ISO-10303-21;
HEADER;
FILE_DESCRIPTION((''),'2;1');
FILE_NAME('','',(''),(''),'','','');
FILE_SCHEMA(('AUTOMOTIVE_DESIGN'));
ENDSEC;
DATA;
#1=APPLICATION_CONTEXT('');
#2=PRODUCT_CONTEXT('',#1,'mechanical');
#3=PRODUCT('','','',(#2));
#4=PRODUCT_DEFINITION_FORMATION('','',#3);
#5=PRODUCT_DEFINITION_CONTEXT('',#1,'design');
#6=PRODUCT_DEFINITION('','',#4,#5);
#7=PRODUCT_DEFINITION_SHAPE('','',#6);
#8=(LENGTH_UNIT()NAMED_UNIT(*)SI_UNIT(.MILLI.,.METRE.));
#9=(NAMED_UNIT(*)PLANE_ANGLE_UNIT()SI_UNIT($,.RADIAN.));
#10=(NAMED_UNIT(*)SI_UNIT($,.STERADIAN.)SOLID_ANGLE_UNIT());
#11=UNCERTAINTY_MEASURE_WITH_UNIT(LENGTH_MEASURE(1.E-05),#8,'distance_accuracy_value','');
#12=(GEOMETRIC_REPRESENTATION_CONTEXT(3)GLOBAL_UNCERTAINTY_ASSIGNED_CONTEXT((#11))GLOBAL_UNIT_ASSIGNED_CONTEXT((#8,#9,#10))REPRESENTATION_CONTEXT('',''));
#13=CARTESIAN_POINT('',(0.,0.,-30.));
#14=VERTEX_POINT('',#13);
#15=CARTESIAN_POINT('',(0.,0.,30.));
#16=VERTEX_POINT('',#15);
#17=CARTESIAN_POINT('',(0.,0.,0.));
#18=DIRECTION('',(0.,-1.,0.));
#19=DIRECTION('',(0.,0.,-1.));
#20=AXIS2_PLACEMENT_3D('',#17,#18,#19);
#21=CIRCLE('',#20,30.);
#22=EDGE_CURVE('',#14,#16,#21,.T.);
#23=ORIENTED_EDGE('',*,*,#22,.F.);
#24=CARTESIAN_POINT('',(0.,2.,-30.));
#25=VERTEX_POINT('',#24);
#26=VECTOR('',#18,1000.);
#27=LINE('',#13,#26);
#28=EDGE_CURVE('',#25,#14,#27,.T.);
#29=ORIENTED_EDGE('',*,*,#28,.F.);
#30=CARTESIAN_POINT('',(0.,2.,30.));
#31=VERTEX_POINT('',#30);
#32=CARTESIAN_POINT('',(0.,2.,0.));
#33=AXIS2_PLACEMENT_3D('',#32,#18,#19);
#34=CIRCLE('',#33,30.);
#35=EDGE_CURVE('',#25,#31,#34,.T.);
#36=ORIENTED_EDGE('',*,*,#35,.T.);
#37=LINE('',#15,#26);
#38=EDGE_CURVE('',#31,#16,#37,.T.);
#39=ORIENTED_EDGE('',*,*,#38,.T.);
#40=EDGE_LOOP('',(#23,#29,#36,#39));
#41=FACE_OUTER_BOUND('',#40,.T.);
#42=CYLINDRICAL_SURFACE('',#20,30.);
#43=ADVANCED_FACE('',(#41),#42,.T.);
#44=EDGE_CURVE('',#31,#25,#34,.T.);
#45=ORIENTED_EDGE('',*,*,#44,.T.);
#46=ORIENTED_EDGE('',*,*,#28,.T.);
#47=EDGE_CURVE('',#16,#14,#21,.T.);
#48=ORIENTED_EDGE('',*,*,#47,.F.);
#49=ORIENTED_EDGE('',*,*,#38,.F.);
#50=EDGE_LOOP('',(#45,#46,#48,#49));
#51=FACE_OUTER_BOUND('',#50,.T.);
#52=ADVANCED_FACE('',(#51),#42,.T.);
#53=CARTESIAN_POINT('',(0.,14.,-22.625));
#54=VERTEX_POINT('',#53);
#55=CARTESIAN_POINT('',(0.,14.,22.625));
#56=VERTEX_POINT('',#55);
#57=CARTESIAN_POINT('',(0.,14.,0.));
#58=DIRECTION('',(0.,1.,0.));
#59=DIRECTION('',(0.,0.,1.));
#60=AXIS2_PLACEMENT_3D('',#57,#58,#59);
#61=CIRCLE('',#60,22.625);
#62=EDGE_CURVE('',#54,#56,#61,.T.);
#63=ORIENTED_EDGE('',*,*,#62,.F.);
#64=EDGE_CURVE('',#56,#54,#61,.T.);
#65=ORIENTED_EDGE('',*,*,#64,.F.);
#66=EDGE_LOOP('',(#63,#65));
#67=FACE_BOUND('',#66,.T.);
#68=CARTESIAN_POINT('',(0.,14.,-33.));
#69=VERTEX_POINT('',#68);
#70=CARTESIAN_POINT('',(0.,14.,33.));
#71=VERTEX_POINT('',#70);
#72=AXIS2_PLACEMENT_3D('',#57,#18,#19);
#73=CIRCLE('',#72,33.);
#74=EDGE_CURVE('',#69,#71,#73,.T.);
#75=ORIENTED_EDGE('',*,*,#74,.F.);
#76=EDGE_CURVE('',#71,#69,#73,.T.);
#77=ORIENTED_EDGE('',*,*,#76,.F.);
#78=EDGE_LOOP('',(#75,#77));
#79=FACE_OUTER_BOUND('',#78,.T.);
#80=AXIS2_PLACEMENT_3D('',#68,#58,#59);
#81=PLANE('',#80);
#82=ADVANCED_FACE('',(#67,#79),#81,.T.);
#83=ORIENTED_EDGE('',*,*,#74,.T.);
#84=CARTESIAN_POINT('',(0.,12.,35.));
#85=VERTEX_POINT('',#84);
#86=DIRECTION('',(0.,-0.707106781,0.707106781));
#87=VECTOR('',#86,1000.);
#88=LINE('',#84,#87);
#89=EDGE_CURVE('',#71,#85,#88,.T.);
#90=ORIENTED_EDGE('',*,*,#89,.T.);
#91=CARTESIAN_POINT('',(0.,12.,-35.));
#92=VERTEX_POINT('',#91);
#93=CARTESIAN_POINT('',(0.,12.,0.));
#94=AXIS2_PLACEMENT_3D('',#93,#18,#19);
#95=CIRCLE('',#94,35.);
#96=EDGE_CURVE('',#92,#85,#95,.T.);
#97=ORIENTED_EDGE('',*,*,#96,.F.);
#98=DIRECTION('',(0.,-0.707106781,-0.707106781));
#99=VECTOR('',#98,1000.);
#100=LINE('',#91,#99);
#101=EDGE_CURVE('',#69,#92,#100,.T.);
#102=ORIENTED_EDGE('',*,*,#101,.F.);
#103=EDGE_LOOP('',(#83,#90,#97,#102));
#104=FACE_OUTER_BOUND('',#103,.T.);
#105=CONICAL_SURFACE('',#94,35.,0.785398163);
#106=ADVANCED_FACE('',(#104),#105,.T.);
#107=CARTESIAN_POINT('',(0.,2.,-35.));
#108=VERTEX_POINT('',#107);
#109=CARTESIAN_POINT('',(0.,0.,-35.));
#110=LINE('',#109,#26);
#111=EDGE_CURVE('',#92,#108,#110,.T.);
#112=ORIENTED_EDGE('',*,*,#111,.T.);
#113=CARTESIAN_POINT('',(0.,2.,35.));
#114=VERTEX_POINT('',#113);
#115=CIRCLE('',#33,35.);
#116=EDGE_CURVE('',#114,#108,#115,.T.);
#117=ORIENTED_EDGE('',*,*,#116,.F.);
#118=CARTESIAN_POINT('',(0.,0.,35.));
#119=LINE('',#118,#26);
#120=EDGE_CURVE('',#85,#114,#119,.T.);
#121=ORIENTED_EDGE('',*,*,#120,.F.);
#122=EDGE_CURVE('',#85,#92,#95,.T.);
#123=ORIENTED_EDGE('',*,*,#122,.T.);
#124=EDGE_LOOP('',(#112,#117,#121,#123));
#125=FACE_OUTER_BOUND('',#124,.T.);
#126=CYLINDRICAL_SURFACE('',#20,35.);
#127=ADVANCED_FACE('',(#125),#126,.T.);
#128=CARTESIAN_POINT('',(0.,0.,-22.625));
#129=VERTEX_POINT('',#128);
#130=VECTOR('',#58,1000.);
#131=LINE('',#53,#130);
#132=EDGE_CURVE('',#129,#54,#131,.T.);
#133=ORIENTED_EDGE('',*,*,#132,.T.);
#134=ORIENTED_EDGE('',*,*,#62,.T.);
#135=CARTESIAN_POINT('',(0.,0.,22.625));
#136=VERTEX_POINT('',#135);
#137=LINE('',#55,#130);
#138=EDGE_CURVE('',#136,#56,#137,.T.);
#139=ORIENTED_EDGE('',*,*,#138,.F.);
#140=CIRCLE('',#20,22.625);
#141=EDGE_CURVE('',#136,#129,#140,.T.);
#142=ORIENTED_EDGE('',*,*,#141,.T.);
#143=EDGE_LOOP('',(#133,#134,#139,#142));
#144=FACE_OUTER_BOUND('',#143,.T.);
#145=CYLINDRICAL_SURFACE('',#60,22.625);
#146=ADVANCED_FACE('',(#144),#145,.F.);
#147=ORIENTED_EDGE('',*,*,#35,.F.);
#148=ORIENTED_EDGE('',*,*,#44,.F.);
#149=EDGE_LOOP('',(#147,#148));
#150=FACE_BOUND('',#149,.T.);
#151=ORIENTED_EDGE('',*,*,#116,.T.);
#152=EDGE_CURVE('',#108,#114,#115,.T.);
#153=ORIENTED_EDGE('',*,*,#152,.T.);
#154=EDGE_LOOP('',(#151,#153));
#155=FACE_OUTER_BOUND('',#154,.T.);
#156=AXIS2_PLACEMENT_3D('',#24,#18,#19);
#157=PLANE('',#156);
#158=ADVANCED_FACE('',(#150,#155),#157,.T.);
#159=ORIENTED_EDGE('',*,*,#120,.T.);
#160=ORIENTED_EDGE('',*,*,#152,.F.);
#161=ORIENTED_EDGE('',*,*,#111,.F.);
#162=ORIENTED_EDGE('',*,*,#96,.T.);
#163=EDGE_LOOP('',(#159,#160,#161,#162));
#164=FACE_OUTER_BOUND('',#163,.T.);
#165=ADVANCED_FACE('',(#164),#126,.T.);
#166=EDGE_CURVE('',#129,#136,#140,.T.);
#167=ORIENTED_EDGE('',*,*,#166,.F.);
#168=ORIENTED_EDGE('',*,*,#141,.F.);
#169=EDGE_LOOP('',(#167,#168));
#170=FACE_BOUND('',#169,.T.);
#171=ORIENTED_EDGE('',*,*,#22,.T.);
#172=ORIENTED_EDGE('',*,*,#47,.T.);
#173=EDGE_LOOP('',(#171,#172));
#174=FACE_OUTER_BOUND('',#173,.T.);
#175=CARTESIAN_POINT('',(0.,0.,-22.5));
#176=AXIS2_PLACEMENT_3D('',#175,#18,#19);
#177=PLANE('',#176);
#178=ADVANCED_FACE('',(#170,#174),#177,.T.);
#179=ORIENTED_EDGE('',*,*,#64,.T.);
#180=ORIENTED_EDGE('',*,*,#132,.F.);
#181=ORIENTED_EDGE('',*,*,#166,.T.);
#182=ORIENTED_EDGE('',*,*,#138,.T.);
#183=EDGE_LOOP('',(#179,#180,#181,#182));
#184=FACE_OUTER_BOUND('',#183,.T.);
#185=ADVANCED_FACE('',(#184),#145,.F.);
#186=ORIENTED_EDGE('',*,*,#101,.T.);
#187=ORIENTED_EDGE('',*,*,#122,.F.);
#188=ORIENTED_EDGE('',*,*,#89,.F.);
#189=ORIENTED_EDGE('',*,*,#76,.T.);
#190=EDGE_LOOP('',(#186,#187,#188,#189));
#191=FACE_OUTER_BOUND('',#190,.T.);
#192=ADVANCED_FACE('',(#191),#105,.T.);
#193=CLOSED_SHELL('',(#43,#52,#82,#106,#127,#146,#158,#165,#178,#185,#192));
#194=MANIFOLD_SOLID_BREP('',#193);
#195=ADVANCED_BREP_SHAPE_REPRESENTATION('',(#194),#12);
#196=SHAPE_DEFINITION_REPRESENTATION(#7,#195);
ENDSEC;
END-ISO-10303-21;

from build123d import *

# Parameters (mm, degrees)
G1_1_2_TAPPED_HOLE1_D     = 45.25
G1_1_2_TAPPED_HOLE1_DEPTH = 102.54
G1_1_2_TAPPED_HOLE1_TIP   = 13.594471505


with BuildPart() as part:
    # Sketch1 → Revolve1 (revolve)
    with BuildSketch(Plane(origin=(0, 0, 0), x_dir=(0, 0, -1), z_dir=(1, 0, 0))):
        Polygon((35, 12), (33, 14), (22.5, 14), (22.5, 0), (30, 0), (30, 2), (35, 2), align=None)
    revolve(axis=Axis((0, 0, 0), (0, 1, 0)))

    # G1-1/2 Tapped Hole1
    with Locations(Plane(origin=(0, 14, 0), x_dir=(1, 0, 0), z_dir=(0, 1, 0))):
        with Locations((0, 0)):
            Hole(G1_1_2_TAPPED_HOLE1_D / 2, depth=G1_1_2_TAPPED_HOLE1_DEPTH)
            with Locations((0, 0, -(G1_1_2_TAPPED_HOLE1_DEPTH + G1_1_2_TAPPED_HOLE1_TIP / 2))):  # 118° drill point
                Cone(0, G1_1_2_TAPPED_HOLE1_D / 2, G1_1_2_TAPPED_HOLE1_TIP, mode=Mode.SUBTRACT)


solid = part.part
